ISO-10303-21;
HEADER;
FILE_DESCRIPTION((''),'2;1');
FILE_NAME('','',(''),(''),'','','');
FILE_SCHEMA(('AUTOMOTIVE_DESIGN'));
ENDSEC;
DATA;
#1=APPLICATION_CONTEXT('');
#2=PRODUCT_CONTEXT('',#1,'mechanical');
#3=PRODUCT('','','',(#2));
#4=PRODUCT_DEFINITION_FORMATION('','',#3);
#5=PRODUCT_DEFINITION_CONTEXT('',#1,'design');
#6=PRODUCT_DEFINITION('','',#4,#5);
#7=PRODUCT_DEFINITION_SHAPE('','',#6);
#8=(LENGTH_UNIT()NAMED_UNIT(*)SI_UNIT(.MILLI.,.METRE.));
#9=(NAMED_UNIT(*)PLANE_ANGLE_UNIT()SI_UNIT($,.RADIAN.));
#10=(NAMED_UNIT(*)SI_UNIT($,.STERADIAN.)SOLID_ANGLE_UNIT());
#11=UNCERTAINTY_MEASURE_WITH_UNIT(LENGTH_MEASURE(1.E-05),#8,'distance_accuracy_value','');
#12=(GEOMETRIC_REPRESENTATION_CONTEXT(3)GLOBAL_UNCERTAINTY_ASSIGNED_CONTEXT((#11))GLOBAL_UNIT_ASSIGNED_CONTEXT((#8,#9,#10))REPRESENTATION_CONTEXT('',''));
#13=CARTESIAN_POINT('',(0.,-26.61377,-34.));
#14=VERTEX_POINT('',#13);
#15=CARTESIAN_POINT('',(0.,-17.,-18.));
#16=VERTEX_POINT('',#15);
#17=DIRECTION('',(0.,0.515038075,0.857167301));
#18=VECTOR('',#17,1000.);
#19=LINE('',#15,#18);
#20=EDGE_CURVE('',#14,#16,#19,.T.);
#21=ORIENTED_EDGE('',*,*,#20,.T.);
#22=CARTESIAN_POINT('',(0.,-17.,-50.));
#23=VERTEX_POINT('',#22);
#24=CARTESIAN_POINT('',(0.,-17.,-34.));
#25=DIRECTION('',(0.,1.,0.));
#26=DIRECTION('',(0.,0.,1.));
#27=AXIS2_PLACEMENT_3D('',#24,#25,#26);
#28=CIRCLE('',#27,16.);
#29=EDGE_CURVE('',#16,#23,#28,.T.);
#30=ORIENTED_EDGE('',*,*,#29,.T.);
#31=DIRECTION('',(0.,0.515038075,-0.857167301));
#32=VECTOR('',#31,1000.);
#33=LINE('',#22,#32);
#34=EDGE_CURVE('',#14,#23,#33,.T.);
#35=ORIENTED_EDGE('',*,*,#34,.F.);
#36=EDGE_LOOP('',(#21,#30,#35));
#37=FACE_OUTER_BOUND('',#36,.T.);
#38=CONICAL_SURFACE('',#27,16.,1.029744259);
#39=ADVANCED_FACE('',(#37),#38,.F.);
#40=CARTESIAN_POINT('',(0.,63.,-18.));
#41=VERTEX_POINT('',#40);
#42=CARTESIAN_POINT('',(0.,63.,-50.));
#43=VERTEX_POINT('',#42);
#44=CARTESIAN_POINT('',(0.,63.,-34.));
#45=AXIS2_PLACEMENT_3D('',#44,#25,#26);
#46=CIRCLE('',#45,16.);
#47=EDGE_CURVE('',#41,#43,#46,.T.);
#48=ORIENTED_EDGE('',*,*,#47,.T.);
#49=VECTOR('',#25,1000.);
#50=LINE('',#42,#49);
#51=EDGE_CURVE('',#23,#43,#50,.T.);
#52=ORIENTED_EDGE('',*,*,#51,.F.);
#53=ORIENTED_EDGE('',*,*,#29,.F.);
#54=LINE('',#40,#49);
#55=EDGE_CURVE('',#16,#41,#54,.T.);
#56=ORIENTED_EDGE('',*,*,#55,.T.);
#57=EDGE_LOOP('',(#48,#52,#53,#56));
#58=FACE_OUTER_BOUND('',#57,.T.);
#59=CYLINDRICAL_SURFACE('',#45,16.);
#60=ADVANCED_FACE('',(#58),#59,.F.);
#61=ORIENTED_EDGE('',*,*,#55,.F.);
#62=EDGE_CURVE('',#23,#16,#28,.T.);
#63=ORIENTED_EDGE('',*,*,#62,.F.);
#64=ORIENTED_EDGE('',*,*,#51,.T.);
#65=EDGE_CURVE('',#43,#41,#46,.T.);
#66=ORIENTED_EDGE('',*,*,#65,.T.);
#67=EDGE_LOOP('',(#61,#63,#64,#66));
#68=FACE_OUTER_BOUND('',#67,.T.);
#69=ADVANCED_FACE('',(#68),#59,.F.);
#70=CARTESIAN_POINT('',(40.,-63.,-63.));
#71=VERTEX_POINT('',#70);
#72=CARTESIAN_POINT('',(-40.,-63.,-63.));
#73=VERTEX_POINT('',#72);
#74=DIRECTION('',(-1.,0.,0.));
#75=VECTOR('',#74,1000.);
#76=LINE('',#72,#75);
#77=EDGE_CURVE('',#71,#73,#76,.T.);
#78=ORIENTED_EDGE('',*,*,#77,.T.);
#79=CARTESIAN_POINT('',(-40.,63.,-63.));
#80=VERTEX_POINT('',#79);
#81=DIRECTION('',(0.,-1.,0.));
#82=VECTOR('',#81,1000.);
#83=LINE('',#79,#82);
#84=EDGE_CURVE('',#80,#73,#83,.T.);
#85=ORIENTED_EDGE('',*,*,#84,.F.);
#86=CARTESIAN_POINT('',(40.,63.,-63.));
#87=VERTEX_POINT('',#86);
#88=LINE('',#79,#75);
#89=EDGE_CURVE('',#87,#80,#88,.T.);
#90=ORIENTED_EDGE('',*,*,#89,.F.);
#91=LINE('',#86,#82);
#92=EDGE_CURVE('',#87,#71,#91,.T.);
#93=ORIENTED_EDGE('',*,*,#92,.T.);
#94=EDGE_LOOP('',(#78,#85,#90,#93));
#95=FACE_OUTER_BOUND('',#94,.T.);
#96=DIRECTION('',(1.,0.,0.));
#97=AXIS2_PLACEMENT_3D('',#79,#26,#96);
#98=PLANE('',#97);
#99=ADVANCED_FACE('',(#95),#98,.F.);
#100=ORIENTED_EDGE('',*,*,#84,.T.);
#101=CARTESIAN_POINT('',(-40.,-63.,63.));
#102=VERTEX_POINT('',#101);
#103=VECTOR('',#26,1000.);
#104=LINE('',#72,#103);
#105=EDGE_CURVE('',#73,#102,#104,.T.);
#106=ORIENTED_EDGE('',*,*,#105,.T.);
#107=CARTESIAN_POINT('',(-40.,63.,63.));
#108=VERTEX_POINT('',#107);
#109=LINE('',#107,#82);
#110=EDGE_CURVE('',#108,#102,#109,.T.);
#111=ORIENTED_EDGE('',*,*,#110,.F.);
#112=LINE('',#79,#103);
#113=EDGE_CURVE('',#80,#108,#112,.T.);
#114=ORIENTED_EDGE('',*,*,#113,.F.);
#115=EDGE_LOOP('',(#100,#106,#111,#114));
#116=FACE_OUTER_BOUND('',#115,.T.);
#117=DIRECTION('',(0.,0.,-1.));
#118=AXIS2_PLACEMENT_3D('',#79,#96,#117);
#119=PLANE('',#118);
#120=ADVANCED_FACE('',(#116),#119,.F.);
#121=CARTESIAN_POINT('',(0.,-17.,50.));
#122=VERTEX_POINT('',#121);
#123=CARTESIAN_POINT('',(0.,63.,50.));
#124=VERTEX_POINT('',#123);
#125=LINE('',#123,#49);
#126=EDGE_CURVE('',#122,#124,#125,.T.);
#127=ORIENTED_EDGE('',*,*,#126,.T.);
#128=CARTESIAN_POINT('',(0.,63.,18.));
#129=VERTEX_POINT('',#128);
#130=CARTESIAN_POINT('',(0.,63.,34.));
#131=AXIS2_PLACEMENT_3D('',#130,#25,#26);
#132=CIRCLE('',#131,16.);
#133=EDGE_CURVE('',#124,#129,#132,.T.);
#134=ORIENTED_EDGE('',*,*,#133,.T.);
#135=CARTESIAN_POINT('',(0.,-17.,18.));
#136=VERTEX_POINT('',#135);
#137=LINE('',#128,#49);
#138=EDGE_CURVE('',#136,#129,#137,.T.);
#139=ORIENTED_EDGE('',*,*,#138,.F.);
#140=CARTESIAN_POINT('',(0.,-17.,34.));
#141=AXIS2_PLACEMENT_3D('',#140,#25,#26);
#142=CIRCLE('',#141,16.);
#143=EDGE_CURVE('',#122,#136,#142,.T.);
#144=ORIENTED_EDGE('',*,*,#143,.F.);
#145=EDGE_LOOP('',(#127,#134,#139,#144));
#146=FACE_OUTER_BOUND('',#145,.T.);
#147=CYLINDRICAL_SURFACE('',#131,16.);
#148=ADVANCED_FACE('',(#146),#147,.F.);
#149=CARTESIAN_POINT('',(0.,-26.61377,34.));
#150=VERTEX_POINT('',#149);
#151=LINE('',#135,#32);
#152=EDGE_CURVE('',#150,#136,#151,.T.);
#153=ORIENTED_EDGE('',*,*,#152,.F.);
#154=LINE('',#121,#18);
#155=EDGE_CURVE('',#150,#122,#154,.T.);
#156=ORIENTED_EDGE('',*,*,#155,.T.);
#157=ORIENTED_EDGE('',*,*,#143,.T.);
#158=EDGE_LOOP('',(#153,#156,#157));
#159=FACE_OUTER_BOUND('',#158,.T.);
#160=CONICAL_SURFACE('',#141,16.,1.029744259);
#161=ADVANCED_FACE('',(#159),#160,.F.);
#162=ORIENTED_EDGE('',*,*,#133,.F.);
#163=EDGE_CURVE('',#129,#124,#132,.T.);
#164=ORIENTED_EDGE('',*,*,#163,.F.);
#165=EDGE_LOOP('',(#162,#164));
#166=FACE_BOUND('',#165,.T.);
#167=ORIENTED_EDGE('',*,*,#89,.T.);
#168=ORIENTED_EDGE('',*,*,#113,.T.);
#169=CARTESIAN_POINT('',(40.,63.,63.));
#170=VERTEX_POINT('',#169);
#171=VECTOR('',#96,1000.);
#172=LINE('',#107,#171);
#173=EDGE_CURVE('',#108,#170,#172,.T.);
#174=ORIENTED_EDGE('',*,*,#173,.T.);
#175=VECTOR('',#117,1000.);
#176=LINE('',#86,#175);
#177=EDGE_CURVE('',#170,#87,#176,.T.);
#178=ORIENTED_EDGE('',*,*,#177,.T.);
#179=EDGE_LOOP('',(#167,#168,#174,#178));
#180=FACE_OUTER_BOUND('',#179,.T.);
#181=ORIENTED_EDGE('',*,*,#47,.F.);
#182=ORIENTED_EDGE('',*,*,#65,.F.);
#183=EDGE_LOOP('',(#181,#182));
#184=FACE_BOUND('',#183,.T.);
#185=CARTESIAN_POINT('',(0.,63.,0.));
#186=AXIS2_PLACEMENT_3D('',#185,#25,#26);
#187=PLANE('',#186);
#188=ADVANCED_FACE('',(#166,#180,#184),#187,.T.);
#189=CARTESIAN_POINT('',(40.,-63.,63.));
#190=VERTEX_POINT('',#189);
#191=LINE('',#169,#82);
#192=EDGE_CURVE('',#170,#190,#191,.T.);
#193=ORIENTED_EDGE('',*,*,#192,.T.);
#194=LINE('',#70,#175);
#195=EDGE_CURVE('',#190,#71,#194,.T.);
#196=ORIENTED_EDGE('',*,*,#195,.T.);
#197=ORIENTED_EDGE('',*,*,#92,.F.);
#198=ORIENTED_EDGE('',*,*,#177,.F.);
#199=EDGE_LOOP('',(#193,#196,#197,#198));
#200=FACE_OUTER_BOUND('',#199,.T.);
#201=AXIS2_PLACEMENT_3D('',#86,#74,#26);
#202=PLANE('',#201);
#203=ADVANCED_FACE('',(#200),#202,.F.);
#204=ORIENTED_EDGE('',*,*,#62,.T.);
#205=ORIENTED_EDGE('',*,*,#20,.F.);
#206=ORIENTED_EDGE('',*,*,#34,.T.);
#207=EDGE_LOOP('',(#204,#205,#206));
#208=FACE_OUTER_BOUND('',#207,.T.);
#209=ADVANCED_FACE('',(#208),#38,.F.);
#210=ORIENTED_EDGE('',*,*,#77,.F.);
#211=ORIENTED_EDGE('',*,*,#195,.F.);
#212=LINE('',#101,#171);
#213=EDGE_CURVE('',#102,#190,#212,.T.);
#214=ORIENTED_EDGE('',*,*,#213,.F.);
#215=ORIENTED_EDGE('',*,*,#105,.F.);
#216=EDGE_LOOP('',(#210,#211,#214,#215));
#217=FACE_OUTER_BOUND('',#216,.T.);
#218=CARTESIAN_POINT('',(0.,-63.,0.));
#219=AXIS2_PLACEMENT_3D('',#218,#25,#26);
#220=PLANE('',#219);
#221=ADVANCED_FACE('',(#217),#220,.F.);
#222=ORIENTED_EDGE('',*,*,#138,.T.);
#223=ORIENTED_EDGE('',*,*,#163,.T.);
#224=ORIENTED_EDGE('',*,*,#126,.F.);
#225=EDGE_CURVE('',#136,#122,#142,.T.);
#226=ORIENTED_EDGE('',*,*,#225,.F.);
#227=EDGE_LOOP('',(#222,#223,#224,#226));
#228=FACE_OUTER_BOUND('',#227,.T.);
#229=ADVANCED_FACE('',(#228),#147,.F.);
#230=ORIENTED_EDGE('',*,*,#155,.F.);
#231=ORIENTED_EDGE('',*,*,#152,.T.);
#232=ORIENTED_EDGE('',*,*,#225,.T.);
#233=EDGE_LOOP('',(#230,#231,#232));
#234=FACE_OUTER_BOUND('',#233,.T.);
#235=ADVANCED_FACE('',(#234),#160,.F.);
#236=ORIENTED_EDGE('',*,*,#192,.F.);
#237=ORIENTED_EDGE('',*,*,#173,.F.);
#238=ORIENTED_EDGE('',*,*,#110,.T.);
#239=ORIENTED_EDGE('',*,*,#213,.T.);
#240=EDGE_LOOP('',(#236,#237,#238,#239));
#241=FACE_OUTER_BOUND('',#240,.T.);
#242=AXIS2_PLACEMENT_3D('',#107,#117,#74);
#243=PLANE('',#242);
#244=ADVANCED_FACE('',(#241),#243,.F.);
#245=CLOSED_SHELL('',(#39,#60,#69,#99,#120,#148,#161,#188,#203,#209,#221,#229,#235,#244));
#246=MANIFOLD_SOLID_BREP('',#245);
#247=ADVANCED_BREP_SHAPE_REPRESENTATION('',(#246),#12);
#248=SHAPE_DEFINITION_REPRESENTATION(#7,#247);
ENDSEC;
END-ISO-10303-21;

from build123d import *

# Parameters (mm, degrees)
SKETCH2_W              = 80
SKETCH2_H              = 126
BOSS_EXTRUDE1_DEPTH    = 63
M36_TAPPED_HOLE1_D     = 32
M36_TAPPED_HOLE1_DEPTH = 80
M36_TAPPED_HOLE1_TIP   = 9.613769904


with BuildPart() as part:
    # Sketch2 → Boss-Extrude1 (new, symmetric)
    with BuildSketch(Plane(origin=(0, 0, 0), x_dir=(1, 0, 0), z_dir=(0, 1, 0))):
        Rectangle(SKETCH2_W, SKETCH2_H)
    extrude(amount=BOSS_EXTRUDE1_DEPTH, both=True)

    # M36 Tapped Hole1
    with Locations(Plane(origin=(0, 63, 0), x_dir=(1, 0, 0), z_dir=(0, 1, 0))):
        with Locations((0, 34), (0, -34)):
            Hole(M36_TAPPED_HOLE1_D / 2, depth=M36_TAPPED_HOLE1_DEPTH)
            with Locations((0, 0, -(M36_TAPPED_HOLE1_DEPTH + M36_TAPPED_HOLE1_TIP / 2))):  # 118° drill point
                Cone(0, M36_TAPPED_HOLE1_D / 2, M36_TAPPED_HOLE1_TIP, mode=Mode.SUBTRACT)


solid = part.part
